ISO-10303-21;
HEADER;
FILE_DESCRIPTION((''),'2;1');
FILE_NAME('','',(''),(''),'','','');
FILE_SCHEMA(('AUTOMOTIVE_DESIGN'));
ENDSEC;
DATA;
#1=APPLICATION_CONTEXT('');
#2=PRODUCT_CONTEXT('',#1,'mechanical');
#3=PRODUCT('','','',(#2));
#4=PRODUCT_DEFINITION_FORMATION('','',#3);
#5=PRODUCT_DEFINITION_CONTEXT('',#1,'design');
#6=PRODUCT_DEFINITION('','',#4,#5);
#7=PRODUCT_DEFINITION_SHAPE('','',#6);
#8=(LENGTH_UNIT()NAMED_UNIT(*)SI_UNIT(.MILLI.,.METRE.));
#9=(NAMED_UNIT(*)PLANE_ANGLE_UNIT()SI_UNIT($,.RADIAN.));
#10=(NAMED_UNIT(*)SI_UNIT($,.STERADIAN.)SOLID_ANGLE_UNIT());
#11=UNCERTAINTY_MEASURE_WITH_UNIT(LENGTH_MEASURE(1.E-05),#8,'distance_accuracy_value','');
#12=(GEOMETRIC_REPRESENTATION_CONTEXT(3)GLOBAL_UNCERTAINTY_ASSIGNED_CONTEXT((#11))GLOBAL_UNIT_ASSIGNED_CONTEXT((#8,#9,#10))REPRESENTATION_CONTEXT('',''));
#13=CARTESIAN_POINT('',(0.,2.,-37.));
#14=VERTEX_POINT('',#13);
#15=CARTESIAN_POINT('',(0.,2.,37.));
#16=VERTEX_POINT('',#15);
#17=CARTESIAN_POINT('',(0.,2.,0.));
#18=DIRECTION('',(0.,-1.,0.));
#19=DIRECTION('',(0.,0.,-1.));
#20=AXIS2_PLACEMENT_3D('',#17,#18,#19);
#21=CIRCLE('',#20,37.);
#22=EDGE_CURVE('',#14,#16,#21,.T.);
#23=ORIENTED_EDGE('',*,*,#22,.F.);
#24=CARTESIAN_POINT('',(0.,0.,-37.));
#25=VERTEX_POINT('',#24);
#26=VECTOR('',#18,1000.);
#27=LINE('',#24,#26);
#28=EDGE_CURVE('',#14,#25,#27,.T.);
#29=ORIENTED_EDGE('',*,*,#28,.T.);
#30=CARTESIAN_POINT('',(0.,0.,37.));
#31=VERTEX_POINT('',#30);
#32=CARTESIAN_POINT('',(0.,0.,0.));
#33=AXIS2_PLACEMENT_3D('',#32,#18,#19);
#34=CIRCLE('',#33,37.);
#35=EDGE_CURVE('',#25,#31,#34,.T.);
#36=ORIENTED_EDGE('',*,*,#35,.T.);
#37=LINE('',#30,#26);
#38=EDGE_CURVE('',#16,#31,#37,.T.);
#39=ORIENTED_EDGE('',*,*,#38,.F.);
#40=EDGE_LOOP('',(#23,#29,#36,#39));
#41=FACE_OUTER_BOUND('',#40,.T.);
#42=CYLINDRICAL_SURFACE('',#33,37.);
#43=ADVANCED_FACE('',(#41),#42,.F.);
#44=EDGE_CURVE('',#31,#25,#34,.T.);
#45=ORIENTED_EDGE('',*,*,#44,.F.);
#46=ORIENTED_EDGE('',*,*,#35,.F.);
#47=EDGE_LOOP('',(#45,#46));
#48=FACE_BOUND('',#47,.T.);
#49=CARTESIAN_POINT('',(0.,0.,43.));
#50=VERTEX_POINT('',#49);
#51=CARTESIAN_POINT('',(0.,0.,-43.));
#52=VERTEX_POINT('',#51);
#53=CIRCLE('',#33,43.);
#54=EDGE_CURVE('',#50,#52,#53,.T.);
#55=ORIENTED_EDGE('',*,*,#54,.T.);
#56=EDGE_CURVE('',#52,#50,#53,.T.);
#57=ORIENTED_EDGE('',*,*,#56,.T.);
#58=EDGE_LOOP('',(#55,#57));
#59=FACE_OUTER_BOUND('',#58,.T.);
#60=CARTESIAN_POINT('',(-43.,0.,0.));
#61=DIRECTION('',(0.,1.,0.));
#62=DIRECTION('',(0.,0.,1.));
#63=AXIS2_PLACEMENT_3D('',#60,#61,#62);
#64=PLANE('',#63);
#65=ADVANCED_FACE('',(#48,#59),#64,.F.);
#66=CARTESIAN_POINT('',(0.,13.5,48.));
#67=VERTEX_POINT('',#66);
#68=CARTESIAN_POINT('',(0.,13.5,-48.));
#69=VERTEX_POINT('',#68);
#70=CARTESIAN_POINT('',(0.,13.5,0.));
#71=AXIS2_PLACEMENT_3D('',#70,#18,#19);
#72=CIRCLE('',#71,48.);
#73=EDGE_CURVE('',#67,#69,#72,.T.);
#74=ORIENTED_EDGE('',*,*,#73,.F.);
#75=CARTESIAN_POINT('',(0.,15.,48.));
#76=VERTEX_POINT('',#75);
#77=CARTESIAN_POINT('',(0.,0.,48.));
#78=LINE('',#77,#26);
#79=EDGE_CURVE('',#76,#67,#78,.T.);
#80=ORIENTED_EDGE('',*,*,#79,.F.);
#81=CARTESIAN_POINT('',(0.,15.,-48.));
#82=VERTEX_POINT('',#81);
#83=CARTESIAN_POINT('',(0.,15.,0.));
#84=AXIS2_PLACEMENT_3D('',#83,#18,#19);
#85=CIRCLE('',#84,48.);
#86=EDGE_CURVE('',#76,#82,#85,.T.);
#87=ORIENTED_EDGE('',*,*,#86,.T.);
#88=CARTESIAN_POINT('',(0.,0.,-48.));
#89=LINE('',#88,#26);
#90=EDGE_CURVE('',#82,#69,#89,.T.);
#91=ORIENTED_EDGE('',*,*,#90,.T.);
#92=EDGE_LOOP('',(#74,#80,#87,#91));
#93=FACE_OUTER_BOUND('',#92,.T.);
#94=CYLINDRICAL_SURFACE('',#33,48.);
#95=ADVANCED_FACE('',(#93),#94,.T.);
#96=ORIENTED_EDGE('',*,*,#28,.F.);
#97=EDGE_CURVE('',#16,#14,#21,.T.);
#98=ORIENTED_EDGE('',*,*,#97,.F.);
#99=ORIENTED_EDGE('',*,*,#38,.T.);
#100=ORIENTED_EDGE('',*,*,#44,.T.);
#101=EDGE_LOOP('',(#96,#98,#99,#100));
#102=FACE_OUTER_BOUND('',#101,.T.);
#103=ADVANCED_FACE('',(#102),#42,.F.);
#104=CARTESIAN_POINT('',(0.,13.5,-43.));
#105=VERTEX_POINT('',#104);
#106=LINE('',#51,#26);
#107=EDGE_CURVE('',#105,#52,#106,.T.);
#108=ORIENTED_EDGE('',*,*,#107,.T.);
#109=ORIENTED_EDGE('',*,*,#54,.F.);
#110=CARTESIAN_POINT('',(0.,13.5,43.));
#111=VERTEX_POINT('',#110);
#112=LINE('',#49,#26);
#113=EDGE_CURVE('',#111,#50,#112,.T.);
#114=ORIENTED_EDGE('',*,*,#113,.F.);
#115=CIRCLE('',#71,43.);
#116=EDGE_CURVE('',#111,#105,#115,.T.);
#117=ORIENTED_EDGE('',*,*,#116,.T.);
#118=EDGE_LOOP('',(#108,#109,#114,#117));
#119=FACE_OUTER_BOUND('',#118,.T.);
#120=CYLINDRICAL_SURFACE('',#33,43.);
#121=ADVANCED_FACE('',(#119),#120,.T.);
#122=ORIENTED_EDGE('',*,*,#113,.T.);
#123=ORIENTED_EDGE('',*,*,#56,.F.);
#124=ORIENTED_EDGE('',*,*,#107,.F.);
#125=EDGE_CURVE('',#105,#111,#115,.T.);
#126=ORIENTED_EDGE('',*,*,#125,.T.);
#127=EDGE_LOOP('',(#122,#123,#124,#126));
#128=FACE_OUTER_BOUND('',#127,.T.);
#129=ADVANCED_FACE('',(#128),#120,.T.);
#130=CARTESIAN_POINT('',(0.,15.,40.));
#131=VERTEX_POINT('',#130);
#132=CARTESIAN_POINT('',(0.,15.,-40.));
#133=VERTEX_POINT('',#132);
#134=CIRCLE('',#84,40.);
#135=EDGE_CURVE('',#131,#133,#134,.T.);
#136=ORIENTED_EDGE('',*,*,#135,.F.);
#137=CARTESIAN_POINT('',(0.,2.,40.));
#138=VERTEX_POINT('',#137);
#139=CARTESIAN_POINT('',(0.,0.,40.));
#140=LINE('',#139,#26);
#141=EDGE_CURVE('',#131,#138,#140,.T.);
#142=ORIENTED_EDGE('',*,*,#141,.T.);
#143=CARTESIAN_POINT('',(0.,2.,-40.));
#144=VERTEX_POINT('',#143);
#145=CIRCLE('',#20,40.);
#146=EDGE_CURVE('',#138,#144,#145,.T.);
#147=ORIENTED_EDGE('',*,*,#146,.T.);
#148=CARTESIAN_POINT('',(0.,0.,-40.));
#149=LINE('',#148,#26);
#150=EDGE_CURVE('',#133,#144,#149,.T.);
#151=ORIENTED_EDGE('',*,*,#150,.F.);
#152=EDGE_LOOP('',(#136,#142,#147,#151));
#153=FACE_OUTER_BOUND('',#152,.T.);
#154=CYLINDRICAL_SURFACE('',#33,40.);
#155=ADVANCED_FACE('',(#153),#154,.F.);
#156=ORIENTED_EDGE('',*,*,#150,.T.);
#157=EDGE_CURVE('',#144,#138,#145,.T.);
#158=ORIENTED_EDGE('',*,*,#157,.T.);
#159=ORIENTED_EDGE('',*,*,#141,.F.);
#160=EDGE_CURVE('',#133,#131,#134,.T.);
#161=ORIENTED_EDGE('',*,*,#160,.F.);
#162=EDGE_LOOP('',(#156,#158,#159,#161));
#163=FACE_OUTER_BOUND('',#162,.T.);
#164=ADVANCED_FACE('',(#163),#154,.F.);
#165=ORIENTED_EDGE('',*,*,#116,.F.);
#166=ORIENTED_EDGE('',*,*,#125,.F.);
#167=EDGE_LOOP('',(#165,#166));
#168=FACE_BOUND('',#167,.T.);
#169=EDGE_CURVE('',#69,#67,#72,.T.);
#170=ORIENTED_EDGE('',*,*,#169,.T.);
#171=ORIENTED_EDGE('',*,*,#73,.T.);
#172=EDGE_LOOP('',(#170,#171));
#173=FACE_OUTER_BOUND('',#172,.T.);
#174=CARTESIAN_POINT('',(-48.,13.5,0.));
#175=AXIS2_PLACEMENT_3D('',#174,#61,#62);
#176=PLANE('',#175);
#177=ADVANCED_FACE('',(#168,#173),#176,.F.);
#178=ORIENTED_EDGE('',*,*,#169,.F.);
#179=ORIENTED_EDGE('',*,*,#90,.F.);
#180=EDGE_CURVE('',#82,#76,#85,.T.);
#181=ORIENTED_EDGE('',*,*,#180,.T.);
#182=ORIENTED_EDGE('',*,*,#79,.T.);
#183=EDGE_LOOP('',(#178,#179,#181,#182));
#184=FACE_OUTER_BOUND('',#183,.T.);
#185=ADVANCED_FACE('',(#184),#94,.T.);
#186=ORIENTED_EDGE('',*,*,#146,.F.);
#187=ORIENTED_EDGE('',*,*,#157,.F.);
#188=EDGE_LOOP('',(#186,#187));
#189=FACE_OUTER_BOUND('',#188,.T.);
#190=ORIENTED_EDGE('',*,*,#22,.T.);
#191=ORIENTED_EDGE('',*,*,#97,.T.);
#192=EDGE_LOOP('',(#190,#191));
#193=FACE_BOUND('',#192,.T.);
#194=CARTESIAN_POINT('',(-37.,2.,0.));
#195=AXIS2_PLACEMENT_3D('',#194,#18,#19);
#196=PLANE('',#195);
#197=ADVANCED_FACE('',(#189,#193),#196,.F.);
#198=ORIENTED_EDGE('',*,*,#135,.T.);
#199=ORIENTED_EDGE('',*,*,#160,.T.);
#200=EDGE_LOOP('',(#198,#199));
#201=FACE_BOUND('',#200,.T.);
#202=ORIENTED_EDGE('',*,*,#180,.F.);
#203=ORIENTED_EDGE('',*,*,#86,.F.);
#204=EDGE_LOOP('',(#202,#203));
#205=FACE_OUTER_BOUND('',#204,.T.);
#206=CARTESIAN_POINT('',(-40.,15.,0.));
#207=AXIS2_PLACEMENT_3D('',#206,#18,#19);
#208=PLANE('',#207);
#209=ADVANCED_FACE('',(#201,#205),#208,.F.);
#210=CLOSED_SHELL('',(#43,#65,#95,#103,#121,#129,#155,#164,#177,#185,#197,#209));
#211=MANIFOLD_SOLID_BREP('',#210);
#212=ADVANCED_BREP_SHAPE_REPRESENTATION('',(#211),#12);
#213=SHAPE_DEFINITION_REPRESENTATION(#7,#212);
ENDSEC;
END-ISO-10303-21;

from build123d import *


with BuildPart() as part:
    # 草图1 → 旋转1 (revolve)
    with BuildSketch(Plane.XY, mode=Mode.PRIVATE) as revolve_1_sk:
        Polygon((-37, 0), (-37, 2), (-40, 2), (-40, 15), (-48, 15), (-48, 13.5), (-43, 13.5), (-43, 0), align=None)
    revolve(revolve_1_sk.sketch.rotate(Axis((0, 0, 0), (0, 1, 0)), 270), axis=Axis((0, 0, 0), (0, 1, 0)))


solid = part.part
